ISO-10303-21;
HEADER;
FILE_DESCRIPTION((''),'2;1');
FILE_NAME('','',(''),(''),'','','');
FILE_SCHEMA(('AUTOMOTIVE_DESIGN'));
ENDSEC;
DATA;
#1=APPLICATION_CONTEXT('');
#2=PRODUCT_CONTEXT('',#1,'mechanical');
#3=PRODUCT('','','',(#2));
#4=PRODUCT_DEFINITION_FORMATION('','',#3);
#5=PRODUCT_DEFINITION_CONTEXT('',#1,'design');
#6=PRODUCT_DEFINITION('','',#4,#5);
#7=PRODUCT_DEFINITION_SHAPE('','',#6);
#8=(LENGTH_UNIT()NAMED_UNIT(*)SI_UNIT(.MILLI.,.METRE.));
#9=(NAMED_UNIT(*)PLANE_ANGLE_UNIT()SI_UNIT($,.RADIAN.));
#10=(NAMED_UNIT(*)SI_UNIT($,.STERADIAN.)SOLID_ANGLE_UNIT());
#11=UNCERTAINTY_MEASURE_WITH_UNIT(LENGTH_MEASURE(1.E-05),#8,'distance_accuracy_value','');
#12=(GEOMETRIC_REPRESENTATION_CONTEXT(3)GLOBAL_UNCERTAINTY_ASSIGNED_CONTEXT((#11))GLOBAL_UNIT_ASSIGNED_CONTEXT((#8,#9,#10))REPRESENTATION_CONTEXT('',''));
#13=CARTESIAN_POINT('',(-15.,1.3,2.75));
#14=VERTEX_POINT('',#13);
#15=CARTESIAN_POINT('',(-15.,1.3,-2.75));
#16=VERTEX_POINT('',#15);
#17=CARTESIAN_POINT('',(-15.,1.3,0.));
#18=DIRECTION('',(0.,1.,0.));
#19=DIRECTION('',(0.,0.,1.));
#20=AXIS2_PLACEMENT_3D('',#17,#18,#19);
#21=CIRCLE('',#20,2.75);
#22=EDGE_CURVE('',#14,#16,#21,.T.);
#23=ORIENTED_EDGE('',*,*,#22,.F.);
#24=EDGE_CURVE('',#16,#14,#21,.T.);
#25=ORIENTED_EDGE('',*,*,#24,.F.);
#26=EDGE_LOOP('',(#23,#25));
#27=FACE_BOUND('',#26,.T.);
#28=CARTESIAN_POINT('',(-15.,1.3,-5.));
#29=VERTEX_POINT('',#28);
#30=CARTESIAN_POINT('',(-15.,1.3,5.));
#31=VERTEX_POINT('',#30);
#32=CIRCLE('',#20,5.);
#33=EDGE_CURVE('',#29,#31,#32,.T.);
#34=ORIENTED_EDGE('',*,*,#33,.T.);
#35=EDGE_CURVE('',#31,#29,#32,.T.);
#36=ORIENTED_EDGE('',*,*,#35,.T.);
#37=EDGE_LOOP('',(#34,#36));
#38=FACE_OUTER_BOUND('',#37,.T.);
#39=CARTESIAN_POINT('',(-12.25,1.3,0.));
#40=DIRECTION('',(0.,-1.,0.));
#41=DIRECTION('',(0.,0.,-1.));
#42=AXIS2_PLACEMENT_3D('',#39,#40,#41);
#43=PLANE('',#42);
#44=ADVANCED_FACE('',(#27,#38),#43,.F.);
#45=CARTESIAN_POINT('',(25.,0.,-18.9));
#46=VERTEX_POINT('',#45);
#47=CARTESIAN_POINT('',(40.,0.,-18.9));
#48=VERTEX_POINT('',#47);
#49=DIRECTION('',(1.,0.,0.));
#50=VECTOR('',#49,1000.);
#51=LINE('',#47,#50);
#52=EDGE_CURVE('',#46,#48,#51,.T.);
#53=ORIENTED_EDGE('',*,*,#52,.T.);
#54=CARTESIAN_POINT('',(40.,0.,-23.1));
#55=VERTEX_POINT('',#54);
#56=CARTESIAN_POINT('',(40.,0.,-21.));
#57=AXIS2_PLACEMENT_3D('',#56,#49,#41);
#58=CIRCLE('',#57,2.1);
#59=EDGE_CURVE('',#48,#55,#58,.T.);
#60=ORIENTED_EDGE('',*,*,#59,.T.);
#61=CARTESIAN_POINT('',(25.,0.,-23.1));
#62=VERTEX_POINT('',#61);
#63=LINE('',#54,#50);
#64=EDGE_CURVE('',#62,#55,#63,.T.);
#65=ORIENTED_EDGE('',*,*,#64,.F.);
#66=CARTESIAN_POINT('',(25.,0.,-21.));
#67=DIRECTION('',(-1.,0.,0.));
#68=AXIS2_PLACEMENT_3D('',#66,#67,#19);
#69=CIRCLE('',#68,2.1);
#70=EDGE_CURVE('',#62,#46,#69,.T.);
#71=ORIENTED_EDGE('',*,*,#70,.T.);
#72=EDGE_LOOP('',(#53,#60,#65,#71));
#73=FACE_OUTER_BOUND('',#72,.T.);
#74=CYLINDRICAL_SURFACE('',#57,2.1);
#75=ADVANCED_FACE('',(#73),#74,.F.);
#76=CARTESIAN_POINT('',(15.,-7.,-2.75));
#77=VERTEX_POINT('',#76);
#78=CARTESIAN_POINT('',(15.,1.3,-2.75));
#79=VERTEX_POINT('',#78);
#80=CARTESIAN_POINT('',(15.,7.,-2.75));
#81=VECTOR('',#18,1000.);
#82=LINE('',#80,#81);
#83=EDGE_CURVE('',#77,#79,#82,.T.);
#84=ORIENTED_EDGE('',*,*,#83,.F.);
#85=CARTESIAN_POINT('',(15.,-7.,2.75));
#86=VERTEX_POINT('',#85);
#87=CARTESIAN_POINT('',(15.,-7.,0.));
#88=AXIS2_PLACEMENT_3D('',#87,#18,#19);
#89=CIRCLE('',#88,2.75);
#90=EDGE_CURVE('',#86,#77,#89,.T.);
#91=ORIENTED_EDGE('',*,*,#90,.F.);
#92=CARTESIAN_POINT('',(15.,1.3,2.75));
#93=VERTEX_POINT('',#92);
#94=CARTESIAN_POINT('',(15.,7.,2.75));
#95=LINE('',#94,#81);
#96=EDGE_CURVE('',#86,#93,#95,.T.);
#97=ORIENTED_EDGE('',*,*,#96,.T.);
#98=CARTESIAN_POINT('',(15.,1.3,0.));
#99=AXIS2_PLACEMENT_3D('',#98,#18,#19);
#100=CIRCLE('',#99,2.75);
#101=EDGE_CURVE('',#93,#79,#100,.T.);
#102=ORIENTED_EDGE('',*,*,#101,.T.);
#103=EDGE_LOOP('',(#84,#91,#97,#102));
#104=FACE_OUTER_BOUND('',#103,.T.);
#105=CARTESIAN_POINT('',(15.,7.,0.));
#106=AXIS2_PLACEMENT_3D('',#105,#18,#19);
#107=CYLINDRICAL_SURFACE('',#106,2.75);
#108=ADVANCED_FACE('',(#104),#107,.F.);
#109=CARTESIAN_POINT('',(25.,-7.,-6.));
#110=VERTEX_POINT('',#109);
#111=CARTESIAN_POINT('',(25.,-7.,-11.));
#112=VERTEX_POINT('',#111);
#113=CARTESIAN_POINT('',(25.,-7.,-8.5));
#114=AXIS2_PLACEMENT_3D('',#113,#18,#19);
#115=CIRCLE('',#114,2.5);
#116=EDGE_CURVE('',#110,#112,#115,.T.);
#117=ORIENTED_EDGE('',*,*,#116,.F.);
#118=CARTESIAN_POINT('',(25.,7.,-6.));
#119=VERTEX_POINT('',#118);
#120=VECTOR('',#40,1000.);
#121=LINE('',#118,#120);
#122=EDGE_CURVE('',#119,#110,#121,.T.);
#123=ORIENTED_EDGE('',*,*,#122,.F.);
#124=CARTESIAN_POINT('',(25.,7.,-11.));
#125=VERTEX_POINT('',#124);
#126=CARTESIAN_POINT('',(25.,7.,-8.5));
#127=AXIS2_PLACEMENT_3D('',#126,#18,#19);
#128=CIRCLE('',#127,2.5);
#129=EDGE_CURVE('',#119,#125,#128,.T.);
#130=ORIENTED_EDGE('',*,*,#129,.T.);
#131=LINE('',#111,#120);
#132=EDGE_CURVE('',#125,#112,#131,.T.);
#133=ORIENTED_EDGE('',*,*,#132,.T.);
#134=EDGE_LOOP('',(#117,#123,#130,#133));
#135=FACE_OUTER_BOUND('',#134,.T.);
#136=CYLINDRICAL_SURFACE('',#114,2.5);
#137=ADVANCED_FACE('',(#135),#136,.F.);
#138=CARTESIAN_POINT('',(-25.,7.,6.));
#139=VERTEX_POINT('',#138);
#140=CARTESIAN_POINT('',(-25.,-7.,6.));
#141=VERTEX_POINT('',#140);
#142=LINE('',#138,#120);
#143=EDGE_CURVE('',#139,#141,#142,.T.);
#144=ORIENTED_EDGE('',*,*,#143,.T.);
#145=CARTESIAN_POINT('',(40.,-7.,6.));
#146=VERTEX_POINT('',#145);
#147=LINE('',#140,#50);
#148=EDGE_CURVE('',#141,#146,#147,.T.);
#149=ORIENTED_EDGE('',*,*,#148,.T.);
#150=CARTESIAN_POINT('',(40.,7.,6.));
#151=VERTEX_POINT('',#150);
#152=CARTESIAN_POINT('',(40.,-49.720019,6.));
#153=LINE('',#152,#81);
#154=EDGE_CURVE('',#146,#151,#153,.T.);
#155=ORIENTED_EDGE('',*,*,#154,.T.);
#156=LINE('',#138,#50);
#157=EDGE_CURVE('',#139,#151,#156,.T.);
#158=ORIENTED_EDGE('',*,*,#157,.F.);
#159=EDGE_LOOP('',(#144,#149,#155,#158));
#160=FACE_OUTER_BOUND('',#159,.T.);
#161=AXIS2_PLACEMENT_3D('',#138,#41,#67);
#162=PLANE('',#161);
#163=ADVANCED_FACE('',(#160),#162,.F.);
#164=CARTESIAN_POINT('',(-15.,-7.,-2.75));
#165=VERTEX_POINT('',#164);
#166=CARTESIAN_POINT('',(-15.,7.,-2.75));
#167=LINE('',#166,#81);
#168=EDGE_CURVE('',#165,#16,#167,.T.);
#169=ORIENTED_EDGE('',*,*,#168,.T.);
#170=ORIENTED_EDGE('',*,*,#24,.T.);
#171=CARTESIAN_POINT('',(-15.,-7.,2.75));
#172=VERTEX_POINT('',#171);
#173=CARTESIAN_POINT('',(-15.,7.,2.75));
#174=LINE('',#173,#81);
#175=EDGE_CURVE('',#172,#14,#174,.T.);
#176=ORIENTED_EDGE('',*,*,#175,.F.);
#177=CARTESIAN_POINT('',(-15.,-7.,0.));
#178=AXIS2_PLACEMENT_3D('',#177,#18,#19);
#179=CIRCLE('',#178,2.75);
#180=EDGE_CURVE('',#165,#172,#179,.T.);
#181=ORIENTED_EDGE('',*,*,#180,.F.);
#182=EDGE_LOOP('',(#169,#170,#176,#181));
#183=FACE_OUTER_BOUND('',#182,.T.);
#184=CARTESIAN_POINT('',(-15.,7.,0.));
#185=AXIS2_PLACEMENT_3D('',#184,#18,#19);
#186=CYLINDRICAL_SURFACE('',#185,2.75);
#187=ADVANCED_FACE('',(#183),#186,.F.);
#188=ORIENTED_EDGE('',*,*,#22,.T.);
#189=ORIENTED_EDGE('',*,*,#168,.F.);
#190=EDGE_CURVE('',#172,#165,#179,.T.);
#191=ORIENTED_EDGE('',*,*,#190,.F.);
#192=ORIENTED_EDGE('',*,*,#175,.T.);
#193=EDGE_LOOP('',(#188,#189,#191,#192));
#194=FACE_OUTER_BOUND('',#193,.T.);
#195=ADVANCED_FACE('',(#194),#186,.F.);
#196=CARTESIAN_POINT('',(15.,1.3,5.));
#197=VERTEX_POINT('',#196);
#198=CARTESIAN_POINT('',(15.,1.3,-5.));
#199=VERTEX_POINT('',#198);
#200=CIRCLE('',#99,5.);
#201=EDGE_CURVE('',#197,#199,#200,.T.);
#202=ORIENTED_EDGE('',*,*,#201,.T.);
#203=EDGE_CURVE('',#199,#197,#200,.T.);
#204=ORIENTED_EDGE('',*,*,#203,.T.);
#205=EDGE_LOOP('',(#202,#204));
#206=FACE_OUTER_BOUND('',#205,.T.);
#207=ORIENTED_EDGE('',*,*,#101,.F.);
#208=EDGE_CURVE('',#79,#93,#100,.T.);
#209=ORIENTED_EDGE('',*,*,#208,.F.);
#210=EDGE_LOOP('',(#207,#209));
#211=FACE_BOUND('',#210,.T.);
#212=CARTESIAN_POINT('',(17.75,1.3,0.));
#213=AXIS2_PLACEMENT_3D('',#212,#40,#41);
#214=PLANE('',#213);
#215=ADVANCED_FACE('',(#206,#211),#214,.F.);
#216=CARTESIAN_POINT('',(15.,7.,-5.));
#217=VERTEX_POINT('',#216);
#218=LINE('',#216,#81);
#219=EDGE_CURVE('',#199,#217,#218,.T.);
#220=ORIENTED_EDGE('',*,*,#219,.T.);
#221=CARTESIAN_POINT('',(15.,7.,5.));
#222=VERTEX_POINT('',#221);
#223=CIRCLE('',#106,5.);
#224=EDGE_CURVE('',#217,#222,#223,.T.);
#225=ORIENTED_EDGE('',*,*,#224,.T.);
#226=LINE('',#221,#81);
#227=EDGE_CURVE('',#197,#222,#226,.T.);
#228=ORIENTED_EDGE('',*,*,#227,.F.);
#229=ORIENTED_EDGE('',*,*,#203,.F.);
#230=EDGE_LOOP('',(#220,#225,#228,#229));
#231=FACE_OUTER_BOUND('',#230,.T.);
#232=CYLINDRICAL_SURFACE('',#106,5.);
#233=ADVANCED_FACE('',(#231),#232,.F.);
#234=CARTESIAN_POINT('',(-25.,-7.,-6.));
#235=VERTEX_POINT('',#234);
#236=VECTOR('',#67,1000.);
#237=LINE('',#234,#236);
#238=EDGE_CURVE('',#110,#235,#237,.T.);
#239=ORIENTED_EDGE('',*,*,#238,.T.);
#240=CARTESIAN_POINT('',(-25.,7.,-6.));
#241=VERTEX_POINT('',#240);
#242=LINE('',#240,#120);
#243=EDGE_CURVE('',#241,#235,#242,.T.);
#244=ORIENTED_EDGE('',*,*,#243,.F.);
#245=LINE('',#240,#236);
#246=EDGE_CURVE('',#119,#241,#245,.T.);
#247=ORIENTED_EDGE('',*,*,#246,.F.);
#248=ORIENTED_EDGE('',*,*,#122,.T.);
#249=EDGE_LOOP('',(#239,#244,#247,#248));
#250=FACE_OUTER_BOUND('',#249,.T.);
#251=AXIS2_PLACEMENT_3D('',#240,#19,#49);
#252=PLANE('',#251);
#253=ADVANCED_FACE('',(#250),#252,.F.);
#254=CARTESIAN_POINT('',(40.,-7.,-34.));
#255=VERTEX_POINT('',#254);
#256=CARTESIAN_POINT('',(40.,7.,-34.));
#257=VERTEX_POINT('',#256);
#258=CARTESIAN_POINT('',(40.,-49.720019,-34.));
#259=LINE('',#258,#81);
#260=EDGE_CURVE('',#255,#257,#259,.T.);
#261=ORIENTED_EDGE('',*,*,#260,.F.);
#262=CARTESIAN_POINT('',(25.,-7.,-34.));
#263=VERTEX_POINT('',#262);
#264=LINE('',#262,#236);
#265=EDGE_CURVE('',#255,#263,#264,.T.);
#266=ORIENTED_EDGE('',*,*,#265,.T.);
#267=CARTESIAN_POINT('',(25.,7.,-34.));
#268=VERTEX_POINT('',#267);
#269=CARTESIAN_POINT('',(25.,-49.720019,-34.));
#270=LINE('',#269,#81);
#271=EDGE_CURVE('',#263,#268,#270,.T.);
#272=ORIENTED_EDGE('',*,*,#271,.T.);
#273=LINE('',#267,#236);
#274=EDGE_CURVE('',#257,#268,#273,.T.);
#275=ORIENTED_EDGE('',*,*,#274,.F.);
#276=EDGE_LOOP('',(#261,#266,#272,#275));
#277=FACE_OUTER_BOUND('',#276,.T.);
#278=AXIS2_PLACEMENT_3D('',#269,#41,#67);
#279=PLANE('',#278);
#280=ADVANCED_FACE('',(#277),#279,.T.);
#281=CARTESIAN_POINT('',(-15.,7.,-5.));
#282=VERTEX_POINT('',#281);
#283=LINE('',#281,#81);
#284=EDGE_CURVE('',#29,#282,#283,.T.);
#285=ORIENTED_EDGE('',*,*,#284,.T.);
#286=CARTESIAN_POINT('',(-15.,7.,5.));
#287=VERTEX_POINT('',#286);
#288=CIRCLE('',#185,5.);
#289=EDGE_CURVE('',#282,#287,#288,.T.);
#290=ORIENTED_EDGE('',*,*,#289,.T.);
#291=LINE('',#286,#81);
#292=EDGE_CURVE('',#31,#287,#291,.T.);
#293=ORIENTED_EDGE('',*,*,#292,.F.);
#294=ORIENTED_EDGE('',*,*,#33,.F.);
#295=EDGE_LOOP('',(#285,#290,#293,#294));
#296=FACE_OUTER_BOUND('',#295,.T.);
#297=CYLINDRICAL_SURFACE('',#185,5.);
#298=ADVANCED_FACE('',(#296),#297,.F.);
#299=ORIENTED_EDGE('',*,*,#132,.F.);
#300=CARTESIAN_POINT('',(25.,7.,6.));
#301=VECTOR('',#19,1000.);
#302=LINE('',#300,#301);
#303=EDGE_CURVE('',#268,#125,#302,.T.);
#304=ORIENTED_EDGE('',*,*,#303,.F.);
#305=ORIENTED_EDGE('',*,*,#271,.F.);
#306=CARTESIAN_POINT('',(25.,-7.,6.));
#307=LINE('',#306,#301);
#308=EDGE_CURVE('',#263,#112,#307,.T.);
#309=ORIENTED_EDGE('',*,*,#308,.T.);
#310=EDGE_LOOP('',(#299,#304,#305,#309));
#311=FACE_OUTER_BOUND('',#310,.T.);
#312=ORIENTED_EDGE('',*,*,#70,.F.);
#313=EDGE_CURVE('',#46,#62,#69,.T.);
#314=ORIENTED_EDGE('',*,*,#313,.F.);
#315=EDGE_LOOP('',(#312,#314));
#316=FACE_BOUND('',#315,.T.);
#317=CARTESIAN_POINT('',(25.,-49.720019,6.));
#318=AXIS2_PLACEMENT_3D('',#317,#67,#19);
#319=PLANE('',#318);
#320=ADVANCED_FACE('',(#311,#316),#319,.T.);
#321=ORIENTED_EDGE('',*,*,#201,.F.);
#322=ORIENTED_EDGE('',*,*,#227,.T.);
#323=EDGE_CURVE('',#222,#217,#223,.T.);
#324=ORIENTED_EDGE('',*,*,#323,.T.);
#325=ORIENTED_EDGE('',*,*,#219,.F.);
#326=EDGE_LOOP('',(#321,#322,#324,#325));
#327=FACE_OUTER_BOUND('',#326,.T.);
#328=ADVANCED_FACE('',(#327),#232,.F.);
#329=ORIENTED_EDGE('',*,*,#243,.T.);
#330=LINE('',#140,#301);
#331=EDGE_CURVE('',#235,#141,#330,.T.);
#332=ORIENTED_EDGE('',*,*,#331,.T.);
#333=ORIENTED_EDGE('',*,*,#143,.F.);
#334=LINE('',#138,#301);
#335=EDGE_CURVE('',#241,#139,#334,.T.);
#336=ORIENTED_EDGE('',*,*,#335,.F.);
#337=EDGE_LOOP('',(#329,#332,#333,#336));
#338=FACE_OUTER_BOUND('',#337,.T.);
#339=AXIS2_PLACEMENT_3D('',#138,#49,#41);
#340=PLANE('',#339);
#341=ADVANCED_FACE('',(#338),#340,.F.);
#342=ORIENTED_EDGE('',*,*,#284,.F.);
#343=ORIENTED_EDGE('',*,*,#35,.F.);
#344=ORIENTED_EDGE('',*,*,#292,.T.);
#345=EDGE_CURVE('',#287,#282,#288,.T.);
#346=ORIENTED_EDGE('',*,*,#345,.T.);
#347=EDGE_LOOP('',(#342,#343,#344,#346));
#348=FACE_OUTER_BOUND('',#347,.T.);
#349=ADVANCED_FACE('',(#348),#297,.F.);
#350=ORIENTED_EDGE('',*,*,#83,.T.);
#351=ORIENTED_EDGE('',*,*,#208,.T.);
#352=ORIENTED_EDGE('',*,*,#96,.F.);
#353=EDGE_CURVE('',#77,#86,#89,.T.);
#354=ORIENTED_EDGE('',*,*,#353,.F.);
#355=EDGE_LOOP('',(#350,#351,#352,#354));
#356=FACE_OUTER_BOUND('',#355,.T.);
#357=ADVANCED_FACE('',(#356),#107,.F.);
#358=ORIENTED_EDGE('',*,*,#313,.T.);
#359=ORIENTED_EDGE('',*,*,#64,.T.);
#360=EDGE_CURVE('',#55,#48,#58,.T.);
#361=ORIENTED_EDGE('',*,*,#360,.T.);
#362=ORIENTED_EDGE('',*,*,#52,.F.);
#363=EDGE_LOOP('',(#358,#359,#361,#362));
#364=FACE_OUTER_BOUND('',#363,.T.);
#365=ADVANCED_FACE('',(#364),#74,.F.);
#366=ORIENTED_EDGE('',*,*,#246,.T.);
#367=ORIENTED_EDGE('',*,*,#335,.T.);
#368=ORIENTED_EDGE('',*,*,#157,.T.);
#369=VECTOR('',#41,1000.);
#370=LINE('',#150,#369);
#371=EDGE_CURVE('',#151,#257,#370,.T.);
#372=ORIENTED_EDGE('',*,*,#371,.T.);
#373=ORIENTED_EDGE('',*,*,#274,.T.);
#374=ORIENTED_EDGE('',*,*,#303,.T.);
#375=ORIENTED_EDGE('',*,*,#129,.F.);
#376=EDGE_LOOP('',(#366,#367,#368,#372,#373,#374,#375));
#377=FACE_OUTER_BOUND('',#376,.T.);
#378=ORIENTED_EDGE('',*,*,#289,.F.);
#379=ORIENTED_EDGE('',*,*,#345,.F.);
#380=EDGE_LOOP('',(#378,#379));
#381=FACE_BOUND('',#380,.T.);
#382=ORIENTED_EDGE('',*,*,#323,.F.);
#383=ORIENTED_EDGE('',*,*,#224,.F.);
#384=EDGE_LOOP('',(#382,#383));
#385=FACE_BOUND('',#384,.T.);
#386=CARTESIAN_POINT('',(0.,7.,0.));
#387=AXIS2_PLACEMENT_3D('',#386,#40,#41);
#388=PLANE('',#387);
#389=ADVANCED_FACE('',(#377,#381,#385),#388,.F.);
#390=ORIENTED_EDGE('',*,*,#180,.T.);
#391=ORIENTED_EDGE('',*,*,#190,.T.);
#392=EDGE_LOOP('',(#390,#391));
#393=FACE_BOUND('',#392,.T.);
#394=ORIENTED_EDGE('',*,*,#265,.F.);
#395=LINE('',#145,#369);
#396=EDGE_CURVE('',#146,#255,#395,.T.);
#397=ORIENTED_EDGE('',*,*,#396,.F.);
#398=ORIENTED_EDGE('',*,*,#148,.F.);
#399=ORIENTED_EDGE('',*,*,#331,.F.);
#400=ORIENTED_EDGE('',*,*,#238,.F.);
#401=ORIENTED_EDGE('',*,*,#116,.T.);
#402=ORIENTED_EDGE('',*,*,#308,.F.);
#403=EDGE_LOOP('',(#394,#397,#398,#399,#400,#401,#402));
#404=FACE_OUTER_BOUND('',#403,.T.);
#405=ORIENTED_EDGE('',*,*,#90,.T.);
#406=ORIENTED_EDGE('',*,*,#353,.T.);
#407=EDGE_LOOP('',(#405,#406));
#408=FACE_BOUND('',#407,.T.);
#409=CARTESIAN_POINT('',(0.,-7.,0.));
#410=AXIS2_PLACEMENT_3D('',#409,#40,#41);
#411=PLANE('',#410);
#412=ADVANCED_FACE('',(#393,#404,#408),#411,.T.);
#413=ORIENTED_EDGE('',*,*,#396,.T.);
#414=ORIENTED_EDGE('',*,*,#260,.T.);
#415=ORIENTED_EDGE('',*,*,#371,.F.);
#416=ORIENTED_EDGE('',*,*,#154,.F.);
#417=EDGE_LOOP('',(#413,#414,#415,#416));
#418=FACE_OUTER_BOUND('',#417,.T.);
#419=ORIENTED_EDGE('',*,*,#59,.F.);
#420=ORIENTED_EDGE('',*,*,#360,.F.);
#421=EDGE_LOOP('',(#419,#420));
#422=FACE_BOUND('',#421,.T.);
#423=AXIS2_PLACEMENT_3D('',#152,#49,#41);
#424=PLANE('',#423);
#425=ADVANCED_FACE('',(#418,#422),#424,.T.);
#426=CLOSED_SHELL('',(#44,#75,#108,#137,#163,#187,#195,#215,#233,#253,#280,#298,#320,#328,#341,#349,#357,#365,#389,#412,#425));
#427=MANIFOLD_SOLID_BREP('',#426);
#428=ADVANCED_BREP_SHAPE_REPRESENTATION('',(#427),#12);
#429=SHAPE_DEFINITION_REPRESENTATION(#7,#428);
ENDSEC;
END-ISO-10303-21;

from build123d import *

# Parameters (mm, degrees)
SKETCH1_W                                           = 50
SKETCH1_H                                           = 12
BOSS_EXTRUDE1_DEPTH                                 = 7
HOLE_SIZE_PER_SOCKET_HEAD_CAP_SCREW_TYP_D           = 5.5
HOLE_SIZE_PER_SOCKET_HEAD_CAP_SCREW_TYP_CBORE_D     = 10
HOLE_SIZE_PER_SOCKET_HEAD_CAP_SCREW_TYP_CBORE_DEPTH = 5.7
SKETCH4_W                                           = 15
SKETCH4_H                                           = 40
BOSS_EXTRUDE2_DEPTH                                 = 14
M5_TAPPED_HOLE1_D                                   = 4.2
SKETCH8_R                                           = 2.5
CUT_EXTRUDE1_DEPTH                                  = 55.332310829


with BuildPart() as part:
    # Sketch1 → Boss-Extrude1 (new, symmetric)
    with BuildSketch(Plane(origin=(0, 0, 0), x_dir=(1, 0, 0), z_dir=(0, 1, 0))):
        Rectangle(SKETCH1_W, SKETCH1_H)
    extrude(amount=BOSS_EXTRUDE1_DEPTH, both=True)

    # Hole Size (per socket head cap screw type)1 (through all)
    with Locations(Plane(origin=(0, 7, 0), x_dir=(1, 0, 0), z_dir=(0, 1, 0))):
        with Locations((15, 0), (-15, 0)):
            CounterBoreHole(HOLE_SIZE_PER_SOCKET_HEAD_CAP_SCREW_TYP_D / 2, HOLE_SIZE_PER_SOCKET_HEAD_CAP_SCREW_TYP_CBORE_D / 2, HOLE_SIZE_PER_SOCKET_HEAD_CAP_SCREW_TYP_CBORE_DEPTH)

    # Sketch4 → Boss-Extrude2 (add)
    with BuildSketch(Plane(origin=(0, 7, 0), x_dir=(1, 0, 0), z_dir=(0, 1, 0))):
        with Locations((32.5, 14)):
            Rectangle(SKETCH4_W, SKETCH4_H)
    extrude(amount=-BOSS_EXTRUDE2_DEPTH)

    # M5 Tapped Hole1 (through all)
    with Locations(Plane(origin=(40, 0, 0), x_dir=(0, 0, -1), z_dir=(1, 0, 0))):
        with Locations((21, 0)):
            Hole(M5_TAPPED_HOLE1_D / 2)

    # Sketch8 → Cut-Extrude1 (cut, through all)
    with BuildSketch(Plane(origin=(0, 7, 0), x_dir=(1, 0, 0), z_dir=(0, 1, 0))):
        with Locations((25, 8.5)):
            Circle(SKETCH8_R)
    extrude(amount=-CUT_EXTRUDE1_DEPTH, mode=Mode.SUBTRACT)


solid = part.part
